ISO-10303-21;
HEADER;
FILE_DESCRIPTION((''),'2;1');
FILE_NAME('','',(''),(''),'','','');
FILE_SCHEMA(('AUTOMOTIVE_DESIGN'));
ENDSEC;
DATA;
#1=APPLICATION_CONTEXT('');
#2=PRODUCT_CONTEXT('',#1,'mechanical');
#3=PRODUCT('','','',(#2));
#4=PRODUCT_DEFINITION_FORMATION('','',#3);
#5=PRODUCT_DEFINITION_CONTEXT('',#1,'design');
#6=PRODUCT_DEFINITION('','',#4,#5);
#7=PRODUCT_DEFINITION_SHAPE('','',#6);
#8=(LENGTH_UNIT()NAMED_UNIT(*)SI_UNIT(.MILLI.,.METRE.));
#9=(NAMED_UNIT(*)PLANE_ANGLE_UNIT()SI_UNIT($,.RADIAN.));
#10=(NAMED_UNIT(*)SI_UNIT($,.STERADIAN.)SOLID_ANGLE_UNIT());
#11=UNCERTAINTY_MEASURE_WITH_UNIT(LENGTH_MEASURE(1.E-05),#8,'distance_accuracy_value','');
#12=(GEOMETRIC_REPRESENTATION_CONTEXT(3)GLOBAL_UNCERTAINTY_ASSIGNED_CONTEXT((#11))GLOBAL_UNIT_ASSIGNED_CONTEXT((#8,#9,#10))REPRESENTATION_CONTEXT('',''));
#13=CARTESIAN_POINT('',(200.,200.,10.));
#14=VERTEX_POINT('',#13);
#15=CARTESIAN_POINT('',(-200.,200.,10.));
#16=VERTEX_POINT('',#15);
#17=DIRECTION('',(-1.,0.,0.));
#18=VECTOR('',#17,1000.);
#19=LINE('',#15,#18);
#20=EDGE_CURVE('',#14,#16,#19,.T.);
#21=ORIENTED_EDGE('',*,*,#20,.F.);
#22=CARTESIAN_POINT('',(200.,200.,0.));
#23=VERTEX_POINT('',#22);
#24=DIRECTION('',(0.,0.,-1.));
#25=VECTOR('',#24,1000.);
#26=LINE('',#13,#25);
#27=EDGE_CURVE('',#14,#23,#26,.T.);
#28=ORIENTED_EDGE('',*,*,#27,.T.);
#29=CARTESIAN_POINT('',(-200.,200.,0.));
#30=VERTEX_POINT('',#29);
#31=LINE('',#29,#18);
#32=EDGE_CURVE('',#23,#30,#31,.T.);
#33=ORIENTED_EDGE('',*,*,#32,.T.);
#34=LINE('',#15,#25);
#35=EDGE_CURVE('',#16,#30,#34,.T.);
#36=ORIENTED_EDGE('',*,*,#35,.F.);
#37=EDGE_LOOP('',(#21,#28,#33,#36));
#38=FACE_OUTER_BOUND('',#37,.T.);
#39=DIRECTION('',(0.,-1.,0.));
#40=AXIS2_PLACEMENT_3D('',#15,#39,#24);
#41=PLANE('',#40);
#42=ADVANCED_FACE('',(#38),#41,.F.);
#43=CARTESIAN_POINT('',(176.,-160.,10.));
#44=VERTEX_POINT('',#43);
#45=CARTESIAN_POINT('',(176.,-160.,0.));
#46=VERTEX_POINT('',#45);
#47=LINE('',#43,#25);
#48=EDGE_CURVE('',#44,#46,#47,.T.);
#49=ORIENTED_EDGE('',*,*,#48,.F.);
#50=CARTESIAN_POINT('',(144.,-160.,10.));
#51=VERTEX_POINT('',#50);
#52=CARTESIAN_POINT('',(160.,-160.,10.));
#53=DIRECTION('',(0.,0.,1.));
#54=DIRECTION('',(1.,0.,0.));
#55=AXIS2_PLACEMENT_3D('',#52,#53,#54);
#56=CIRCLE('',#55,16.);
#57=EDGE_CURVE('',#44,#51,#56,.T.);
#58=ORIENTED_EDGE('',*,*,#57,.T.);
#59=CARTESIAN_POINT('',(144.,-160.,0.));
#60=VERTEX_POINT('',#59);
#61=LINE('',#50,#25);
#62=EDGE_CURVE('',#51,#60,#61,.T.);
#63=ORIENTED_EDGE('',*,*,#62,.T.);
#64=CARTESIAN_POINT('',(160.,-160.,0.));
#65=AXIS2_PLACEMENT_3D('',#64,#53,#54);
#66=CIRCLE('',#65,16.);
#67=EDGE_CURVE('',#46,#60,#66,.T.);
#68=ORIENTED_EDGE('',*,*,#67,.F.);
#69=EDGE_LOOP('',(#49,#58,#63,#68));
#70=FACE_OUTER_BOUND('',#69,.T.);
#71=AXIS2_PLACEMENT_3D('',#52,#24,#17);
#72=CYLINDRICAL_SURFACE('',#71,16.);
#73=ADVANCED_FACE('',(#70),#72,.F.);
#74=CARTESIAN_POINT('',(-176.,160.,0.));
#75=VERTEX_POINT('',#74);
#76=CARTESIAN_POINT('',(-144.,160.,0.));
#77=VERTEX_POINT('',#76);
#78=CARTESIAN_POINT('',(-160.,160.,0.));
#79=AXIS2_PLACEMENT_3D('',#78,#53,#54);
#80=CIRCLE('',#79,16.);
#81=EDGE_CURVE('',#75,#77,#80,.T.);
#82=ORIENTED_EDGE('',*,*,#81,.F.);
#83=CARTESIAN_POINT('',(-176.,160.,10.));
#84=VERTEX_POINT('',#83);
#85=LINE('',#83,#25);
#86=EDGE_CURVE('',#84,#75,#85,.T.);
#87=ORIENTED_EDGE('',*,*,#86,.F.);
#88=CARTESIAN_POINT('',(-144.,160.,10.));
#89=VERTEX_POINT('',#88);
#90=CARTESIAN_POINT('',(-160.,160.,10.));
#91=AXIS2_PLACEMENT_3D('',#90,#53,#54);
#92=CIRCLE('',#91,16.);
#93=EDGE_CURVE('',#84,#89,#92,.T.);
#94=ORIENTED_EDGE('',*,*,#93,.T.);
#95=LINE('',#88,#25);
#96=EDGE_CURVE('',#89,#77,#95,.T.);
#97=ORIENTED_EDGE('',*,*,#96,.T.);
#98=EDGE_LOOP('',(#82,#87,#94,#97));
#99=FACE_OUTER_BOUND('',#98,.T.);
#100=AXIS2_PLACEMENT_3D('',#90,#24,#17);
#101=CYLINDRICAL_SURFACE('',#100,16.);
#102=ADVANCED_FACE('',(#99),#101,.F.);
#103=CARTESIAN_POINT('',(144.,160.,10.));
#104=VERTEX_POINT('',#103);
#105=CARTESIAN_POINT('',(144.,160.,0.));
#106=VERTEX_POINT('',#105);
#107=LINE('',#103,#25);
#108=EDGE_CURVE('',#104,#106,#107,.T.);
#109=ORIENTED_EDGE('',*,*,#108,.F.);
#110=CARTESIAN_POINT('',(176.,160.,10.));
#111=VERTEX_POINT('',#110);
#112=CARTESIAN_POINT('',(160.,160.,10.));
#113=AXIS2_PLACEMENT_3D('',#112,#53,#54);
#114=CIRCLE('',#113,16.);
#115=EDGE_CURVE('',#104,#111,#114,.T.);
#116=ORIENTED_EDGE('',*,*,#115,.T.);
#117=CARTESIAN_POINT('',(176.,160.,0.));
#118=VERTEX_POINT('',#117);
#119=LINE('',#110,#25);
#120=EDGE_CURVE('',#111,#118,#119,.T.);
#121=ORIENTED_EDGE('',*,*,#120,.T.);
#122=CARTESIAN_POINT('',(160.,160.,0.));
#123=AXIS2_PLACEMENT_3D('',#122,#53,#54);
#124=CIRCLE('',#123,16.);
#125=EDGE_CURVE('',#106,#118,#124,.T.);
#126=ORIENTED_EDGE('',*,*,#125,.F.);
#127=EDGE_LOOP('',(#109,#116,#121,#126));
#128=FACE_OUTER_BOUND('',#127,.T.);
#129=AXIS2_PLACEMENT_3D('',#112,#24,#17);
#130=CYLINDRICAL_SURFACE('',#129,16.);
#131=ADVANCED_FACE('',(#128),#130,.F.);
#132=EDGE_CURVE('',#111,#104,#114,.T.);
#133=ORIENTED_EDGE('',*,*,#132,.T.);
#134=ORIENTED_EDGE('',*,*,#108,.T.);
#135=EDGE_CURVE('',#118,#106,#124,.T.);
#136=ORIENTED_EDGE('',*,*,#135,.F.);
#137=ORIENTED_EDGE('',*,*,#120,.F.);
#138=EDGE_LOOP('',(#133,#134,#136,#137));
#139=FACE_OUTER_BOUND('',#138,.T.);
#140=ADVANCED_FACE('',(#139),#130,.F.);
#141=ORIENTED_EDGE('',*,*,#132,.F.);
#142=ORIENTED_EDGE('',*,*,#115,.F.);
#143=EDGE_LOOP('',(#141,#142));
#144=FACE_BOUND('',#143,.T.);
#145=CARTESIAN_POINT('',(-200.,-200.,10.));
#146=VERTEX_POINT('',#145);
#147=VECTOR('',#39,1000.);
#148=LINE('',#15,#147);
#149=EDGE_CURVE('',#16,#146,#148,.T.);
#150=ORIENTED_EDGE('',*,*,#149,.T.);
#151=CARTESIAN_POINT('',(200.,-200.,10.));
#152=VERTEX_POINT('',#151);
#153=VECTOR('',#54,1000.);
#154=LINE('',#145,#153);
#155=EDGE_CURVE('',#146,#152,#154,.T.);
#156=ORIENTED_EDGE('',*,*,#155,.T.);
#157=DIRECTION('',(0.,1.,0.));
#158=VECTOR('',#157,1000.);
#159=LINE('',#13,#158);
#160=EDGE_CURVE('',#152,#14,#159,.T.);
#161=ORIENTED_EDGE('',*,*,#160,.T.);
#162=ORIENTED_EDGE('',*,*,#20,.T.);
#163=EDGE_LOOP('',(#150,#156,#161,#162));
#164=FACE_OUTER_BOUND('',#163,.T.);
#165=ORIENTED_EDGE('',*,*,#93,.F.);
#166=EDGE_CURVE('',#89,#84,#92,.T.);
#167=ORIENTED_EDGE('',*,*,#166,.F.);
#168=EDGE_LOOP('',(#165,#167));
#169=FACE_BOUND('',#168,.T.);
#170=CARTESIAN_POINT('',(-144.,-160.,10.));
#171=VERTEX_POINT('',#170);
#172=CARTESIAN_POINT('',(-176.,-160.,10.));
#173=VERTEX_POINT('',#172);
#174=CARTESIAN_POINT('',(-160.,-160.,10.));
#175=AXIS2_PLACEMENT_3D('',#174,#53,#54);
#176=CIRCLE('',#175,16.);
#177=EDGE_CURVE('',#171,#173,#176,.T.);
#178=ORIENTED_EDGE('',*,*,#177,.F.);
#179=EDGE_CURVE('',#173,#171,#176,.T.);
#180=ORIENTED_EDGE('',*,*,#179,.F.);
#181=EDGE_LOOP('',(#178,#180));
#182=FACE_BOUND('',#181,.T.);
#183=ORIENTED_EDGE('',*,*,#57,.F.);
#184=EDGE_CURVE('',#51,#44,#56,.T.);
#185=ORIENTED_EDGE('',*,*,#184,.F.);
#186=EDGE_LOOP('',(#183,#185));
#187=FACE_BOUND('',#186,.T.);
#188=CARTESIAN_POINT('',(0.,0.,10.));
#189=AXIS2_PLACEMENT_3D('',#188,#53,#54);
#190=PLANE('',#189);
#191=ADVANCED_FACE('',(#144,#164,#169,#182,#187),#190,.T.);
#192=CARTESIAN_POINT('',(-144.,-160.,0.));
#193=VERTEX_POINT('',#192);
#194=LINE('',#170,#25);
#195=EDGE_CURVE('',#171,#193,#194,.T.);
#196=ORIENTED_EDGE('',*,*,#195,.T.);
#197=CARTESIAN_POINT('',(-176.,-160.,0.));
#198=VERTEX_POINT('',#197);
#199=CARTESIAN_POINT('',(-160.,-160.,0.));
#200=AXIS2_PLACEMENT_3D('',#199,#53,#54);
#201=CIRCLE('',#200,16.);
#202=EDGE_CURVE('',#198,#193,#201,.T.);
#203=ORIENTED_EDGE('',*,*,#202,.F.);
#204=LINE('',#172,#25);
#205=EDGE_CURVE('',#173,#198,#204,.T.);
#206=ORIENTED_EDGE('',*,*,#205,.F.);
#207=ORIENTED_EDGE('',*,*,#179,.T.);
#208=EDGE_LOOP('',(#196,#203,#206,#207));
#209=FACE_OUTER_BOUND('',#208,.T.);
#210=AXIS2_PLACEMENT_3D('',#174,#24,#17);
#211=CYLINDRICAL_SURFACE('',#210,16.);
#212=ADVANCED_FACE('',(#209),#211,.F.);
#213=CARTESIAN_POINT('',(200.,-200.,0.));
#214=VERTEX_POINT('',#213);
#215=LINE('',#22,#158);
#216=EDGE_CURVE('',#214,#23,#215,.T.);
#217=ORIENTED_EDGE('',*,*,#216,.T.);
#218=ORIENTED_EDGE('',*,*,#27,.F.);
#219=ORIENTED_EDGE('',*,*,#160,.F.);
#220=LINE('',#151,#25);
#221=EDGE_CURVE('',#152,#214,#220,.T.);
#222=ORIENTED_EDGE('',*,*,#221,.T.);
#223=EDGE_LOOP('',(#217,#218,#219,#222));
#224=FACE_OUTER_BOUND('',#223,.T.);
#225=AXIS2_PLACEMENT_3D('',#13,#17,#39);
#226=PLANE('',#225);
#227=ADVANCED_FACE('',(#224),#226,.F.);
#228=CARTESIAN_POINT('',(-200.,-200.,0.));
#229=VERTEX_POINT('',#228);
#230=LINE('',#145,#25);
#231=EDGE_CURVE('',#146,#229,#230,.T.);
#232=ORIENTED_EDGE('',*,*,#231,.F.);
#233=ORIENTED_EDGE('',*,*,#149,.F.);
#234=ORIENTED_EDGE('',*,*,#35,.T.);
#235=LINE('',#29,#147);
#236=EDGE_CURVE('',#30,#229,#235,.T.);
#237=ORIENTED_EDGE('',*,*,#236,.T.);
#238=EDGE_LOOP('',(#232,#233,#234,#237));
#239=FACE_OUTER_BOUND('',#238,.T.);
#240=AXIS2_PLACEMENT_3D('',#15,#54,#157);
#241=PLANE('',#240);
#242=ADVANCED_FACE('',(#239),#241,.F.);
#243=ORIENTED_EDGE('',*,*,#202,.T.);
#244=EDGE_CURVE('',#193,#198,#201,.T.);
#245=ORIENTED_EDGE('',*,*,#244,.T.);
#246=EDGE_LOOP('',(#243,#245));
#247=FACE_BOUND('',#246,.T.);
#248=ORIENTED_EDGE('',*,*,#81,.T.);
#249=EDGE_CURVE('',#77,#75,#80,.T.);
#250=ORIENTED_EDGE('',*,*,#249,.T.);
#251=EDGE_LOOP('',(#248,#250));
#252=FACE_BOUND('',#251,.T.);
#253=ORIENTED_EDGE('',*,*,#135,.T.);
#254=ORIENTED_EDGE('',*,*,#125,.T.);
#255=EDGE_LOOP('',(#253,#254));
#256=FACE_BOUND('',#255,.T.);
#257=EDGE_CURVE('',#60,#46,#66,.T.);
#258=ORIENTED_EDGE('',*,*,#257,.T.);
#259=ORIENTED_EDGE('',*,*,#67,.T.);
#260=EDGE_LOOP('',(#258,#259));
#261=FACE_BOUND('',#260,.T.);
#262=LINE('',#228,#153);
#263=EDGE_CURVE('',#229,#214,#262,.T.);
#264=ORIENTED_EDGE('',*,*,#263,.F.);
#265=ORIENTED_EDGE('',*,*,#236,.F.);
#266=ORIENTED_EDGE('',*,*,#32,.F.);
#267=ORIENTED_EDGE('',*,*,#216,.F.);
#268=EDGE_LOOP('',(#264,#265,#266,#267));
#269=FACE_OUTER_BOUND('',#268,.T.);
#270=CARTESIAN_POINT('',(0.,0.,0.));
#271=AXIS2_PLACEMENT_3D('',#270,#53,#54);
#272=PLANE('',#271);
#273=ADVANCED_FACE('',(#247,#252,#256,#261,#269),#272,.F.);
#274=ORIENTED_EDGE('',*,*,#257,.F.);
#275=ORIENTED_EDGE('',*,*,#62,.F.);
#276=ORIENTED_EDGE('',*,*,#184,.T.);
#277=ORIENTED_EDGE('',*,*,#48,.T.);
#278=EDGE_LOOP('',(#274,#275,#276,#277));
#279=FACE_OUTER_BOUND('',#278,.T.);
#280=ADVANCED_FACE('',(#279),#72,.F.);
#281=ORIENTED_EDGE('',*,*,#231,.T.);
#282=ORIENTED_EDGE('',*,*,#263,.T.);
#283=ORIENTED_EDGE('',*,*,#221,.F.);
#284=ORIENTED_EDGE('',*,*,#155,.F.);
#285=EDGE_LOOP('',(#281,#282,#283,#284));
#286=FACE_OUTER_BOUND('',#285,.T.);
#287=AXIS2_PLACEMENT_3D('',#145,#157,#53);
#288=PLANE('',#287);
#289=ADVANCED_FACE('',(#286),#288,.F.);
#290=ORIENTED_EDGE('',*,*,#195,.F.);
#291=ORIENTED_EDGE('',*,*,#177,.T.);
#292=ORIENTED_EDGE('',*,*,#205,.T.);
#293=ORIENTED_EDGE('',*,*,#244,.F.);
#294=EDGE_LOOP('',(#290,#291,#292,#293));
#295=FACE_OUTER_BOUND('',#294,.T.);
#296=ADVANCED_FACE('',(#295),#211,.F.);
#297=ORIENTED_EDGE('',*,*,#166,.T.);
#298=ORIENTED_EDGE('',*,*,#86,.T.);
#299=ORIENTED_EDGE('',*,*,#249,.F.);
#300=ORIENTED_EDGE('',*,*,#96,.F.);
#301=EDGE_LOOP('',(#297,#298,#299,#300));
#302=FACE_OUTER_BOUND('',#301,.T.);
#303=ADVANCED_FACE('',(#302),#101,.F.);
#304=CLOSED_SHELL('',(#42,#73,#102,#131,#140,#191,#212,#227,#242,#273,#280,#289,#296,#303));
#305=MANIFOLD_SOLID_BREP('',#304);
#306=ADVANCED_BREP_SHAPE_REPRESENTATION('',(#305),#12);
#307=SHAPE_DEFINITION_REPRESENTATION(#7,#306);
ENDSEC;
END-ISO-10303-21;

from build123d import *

# Parameters (mm, degrees)
SKETCH1_W           = 400
SKETCH1_H           = 400
SKETCH1_R           = 16
BOSS_EXTRUDE1_DEPTH = 10


with BuildPart() as part:
    # Sketch1 → Boss-Extrude1 (new body)
    with BuildSketch(Plane.XY):
        Rectangle(SKETCH1_W, SKETCH1_H)
        with Locations((-160, 160)):
            Circle(SKETCH1_R, mode=Mode.SUBTRACT)
        with Locations((160, 160)):
            Circle(SKETCH1_R, mode=Mode.SUBTRACT)
        with Locations((160, -160)):
            Circle(SKETCH1_R, mode=Mode.SUBTRACT)
        with Locations((-160, -160)):
            Circle(SKETCH1_R, mode=Mode.SUBTRACT)
    extrude(amount=BOSS_EXTRUDE1_DEPTH)


solid = part.part
